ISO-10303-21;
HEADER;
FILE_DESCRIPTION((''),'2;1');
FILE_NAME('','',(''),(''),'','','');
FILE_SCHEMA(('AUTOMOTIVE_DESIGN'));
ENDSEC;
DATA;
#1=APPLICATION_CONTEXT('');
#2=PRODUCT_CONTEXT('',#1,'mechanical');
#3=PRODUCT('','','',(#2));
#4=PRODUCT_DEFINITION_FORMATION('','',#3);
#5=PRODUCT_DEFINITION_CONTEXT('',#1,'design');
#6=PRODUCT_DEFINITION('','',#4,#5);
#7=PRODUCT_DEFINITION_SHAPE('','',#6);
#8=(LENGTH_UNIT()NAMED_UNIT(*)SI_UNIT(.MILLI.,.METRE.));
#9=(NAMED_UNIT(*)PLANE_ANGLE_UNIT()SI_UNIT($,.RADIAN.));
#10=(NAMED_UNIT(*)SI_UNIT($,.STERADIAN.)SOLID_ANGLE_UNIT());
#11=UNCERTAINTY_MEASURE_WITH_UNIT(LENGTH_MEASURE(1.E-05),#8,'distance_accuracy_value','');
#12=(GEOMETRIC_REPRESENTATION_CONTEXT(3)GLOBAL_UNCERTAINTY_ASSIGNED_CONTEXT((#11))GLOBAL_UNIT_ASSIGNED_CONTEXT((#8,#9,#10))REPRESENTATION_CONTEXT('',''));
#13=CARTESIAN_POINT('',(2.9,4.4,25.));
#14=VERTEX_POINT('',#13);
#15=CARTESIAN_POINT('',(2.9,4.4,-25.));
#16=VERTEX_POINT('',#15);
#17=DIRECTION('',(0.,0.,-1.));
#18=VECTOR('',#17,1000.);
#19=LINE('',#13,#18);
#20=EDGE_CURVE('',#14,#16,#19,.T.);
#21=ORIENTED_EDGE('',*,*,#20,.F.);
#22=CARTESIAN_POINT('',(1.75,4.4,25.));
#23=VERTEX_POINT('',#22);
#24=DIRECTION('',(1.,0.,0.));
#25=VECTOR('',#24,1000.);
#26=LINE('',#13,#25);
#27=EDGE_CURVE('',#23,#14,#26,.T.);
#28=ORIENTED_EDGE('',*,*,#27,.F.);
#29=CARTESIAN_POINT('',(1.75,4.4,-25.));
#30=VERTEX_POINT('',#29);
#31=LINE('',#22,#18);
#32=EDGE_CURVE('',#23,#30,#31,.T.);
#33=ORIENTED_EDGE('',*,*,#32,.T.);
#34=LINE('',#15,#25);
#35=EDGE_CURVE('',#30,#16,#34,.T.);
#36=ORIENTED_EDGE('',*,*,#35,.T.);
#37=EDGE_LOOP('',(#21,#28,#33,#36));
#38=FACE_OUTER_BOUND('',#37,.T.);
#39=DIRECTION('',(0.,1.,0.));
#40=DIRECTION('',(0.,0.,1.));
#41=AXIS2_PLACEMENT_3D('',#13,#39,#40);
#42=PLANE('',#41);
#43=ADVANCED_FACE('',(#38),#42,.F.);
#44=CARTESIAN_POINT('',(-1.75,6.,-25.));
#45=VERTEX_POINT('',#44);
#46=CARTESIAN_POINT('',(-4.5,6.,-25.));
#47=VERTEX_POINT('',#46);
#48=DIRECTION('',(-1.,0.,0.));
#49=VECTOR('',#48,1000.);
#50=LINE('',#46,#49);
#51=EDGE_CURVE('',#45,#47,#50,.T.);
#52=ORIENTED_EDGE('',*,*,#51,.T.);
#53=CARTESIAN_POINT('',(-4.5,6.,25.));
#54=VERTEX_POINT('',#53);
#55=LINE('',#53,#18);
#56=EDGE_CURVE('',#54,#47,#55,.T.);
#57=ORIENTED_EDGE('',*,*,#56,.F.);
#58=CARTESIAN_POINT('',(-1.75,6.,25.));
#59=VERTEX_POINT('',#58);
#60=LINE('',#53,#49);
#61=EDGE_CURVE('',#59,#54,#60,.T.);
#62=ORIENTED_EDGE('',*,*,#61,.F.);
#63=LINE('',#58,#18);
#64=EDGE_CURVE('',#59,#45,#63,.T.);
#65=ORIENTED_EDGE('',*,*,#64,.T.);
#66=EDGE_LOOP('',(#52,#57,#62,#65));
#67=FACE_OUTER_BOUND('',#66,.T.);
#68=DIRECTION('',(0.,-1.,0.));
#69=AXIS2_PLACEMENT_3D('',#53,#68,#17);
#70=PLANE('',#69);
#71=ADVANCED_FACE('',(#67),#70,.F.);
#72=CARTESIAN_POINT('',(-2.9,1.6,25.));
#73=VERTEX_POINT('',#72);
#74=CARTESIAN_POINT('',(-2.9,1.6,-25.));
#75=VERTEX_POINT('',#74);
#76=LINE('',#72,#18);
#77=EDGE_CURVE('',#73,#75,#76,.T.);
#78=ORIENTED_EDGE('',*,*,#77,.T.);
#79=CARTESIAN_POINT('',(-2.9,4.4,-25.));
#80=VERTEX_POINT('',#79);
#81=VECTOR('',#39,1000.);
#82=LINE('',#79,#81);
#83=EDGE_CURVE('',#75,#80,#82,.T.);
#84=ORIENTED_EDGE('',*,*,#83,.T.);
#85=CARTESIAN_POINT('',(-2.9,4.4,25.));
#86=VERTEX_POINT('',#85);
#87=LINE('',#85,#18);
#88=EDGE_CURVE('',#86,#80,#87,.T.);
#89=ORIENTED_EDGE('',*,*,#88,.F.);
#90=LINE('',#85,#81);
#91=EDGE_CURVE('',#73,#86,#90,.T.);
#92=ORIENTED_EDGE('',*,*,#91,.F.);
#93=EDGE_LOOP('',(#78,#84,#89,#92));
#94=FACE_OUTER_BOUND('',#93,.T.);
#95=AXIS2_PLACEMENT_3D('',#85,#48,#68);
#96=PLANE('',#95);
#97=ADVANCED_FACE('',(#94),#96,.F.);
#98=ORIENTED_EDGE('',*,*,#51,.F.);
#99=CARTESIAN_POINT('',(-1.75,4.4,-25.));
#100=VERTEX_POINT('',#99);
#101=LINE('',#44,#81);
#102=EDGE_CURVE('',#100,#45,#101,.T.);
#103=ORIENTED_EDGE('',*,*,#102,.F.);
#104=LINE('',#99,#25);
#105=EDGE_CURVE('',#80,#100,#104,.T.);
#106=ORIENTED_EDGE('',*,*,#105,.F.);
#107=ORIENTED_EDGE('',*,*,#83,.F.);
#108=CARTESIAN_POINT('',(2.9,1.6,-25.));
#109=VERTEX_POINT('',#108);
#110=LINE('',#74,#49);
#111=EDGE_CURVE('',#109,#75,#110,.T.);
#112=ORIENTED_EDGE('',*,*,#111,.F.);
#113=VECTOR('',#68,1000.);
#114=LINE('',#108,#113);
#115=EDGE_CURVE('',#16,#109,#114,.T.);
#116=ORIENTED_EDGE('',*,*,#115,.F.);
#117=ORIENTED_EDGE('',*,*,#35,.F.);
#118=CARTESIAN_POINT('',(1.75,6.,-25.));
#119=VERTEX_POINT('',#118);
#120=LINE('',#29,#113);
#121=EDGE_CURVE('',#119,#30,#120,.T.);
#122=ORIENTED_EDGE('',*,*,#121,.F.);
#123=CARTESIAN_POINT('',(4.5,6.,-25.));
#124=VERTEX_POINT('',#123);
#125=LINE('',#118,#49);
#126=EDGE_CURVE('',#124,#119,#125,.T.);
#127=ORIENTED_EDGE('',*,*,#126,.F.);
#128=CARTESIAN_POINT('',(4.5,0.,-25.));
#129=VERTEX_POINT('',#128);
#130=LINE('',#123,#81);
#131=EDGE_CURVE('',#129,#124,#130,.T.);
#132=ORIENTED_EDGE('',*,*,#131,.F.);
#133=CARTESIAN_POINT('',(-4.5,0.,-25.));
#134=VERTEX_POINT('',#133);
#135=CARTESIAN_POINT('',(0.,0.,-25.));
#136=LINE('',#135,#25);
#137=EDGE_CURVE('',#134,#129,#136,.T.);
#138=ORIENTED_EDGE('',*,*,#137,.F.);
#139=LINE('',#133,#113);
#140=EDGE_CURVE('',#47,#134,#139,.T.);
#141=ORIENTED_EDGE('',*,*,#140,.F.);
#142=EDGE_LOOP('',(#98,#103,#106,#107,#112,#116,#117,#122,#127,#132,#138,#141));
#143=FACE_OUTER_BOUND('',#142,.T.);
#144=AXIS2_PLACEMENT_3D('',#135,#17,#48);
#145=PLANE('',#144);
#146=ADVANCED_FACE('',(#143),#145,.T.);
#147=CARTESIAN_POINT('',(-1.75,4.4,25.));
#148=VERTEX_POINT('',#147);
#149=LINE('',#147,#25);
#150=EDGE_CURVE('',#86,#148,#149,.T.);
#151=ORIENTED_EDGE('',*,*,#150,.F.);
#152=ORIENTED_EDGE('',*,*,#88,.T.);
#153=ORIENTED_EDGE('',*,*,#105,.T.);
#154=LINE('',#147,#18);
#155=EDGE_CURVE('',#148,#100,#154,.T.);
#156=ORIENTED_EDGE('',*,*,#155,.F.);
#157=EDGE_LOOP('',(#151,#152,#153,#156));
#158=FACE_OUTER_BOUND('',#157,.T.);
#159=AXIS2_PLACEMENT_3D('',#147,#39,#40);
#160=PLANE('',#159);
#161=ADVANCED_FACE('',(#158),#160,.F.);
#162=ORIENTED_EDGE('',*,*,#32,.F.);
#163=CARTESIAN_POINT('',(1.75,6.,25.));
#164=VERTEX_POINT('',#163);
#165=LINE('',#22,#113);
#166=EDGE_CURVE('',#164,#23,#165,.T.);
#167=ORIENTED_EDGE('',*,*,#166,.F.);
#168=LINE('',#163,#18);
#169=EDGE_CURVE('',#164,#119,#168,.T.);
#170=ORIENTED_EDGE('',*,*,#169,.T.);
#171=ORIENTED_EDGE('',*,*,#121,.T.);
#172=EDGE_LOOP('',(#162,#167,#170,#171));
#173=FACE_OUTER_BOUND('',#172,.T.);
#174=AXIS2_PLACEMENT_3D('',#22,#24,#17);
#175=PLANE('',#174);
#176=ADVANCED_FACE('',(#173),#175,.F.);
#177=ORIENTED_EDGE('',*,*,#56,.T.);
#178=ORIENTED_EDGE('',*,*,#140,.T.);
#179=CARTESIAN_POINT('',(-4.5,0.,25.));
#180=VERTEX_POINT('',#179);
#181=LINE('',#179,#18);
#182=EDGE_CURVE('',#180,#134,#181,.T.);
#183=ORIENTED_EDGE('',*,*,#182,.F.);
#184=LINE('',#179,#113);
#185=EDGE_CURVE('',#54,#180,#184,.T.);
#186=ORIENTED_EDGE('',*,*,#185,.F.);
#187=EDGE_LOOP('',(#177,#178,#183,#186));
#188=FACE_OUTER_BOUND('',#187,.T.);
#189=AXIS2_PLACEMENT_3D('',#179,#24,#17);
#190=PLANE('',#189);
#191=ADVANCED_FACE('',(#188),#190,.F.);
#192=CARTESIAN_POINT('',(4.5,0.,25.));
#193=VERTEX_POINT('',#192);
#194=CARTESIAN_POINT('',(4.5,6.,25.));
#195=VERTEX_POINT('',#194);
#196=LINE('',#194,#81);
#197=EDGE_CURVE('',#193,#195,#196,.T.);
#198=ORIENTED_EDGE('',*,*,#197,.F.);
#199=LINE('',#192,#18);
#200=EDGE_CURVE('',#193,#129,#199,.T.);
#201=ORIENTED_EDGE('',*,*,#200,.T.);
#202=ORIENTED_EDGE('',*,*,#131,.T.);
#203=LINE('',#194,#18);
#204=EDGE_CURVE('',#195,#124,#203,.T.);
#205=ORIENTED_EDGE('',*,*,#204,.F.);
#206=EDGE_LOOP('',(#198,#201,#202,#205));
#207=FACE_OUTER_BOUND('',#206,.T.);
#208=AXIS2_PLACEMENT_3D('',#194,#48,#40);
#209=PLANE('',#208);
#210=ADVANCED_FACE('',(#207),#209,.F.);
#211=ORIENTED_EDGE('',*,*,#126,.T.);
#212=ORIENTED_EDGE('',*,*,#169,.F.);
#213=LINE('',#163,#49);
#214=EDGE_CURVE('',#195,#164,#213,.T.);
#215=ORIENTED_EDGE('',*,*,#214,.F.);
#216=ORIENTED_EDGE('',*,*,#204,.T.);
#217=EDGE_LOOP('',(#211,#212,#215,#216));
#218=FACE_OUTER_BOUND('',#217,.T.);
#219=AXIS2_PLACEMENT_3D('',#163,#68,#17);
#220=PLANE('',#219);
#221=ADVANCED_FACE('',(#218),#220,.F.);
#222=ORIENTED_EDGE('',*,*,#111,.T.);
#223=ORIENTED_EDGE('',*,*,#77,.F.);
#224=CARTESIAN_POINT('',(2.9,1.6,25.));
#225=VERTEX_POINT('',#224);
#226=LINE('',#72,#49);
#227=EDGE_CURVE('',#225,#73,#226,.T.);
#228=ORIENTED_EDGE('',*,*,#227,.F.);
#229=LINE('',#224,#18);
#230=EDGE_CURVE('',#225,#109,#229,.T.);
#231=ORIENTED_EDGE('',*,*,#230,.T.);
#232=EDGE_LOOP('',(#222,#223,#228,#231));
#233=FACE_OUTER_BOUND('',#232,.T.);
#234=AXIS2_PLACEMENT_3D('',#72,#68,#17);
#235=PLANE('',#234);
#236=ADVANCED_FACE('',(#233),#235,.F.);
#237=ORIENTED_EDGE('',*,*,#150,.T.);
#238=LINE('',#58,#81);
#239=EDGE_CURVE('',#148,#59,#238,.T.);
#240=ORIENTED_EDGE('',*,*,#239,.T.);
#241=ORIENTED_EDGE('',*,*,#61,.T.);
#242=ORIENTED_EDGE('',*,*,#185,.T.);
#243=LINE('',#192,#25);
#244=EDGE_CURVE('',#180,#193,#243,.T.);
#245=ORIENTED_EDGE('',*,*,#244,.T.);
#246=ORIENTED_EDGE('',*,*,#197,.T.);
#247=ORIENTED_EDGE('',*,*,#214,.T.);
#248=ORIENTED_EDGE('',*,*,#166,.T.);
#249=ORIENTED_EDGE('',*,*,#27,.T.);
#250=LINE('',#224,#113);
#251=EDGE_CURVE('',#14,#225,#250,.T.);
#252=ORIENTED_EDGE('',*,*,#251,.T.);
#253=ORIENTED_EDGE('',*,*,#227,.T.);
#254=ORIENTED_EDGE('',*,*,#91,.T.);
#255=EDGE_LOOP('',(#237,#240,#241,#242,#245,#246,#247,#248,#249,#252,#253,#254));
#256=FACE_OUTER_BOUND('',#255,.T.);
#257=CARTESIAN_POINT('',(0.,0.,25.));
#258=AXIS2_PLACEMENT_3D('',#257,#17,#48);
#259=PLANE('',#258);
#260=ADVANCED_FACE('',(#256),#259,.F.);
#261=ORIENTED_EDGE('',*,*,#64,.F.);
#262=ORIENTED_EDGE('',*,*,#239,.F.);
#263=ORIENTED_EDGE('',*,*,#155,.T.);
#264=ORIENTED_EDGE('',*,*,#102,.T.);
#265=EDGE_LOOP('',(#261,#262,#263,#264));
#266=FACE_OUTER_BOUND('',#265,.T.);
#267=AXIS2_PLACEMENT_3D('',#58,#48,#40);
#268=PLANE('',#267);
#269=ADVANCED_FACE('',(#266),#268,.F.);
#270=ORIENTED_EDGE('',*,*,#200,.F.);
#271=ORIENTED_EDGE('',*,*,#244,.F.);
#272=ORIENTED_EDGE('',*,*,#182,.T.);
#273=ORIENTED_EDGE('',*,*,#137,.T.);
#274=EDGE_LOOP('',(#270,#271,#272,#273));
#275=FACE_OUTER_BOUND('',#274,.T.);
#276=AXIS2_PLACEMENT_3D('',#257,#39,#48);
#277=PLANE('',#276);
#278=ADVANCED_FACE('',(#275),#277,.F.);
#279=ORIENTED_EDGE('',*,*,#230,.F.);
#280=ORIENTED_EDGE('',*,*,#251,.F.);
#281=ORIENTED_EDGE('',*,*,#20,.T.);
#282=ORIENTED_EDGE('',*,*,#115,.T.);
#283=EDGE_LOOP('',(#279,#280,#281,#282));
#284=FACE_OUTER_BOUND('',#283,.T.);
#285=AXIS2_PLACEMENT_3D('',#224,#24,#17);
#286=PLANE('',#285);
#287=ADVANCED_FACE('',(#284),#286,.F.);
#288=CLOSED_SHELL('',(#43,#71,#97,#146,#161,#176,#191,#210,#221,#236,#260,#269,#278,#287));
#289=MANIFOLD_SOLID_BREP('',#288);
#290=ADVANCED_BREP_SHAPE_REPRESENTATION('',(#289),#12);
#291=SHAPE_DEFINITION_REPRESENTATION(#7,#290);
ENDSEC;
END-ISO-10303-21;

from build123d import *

# Parameters (mm, degrees)
EXTRUDE_1_DEPTH = 25


with BuildPart() as part:
    # 草图1 → 凸台-拉伸1 (new, symmetric)
    with BuildSketch(Plane.XY):
        Polygon((0, 0), (-4.5, 0), (-4.5, 6), (-1.75, 6), (-1.75, 4.4), (-2.9, 4.4), (-2.9, 1.6), (2.9, 1.6), (2.9, 4.4), (1.75, 4.4), (1.75, 6), (4.5, 6), (4.5, 0), align=None)
    extrude(amount=EXTRUDE_1_DEPTH, both=True)


solid = part.part
